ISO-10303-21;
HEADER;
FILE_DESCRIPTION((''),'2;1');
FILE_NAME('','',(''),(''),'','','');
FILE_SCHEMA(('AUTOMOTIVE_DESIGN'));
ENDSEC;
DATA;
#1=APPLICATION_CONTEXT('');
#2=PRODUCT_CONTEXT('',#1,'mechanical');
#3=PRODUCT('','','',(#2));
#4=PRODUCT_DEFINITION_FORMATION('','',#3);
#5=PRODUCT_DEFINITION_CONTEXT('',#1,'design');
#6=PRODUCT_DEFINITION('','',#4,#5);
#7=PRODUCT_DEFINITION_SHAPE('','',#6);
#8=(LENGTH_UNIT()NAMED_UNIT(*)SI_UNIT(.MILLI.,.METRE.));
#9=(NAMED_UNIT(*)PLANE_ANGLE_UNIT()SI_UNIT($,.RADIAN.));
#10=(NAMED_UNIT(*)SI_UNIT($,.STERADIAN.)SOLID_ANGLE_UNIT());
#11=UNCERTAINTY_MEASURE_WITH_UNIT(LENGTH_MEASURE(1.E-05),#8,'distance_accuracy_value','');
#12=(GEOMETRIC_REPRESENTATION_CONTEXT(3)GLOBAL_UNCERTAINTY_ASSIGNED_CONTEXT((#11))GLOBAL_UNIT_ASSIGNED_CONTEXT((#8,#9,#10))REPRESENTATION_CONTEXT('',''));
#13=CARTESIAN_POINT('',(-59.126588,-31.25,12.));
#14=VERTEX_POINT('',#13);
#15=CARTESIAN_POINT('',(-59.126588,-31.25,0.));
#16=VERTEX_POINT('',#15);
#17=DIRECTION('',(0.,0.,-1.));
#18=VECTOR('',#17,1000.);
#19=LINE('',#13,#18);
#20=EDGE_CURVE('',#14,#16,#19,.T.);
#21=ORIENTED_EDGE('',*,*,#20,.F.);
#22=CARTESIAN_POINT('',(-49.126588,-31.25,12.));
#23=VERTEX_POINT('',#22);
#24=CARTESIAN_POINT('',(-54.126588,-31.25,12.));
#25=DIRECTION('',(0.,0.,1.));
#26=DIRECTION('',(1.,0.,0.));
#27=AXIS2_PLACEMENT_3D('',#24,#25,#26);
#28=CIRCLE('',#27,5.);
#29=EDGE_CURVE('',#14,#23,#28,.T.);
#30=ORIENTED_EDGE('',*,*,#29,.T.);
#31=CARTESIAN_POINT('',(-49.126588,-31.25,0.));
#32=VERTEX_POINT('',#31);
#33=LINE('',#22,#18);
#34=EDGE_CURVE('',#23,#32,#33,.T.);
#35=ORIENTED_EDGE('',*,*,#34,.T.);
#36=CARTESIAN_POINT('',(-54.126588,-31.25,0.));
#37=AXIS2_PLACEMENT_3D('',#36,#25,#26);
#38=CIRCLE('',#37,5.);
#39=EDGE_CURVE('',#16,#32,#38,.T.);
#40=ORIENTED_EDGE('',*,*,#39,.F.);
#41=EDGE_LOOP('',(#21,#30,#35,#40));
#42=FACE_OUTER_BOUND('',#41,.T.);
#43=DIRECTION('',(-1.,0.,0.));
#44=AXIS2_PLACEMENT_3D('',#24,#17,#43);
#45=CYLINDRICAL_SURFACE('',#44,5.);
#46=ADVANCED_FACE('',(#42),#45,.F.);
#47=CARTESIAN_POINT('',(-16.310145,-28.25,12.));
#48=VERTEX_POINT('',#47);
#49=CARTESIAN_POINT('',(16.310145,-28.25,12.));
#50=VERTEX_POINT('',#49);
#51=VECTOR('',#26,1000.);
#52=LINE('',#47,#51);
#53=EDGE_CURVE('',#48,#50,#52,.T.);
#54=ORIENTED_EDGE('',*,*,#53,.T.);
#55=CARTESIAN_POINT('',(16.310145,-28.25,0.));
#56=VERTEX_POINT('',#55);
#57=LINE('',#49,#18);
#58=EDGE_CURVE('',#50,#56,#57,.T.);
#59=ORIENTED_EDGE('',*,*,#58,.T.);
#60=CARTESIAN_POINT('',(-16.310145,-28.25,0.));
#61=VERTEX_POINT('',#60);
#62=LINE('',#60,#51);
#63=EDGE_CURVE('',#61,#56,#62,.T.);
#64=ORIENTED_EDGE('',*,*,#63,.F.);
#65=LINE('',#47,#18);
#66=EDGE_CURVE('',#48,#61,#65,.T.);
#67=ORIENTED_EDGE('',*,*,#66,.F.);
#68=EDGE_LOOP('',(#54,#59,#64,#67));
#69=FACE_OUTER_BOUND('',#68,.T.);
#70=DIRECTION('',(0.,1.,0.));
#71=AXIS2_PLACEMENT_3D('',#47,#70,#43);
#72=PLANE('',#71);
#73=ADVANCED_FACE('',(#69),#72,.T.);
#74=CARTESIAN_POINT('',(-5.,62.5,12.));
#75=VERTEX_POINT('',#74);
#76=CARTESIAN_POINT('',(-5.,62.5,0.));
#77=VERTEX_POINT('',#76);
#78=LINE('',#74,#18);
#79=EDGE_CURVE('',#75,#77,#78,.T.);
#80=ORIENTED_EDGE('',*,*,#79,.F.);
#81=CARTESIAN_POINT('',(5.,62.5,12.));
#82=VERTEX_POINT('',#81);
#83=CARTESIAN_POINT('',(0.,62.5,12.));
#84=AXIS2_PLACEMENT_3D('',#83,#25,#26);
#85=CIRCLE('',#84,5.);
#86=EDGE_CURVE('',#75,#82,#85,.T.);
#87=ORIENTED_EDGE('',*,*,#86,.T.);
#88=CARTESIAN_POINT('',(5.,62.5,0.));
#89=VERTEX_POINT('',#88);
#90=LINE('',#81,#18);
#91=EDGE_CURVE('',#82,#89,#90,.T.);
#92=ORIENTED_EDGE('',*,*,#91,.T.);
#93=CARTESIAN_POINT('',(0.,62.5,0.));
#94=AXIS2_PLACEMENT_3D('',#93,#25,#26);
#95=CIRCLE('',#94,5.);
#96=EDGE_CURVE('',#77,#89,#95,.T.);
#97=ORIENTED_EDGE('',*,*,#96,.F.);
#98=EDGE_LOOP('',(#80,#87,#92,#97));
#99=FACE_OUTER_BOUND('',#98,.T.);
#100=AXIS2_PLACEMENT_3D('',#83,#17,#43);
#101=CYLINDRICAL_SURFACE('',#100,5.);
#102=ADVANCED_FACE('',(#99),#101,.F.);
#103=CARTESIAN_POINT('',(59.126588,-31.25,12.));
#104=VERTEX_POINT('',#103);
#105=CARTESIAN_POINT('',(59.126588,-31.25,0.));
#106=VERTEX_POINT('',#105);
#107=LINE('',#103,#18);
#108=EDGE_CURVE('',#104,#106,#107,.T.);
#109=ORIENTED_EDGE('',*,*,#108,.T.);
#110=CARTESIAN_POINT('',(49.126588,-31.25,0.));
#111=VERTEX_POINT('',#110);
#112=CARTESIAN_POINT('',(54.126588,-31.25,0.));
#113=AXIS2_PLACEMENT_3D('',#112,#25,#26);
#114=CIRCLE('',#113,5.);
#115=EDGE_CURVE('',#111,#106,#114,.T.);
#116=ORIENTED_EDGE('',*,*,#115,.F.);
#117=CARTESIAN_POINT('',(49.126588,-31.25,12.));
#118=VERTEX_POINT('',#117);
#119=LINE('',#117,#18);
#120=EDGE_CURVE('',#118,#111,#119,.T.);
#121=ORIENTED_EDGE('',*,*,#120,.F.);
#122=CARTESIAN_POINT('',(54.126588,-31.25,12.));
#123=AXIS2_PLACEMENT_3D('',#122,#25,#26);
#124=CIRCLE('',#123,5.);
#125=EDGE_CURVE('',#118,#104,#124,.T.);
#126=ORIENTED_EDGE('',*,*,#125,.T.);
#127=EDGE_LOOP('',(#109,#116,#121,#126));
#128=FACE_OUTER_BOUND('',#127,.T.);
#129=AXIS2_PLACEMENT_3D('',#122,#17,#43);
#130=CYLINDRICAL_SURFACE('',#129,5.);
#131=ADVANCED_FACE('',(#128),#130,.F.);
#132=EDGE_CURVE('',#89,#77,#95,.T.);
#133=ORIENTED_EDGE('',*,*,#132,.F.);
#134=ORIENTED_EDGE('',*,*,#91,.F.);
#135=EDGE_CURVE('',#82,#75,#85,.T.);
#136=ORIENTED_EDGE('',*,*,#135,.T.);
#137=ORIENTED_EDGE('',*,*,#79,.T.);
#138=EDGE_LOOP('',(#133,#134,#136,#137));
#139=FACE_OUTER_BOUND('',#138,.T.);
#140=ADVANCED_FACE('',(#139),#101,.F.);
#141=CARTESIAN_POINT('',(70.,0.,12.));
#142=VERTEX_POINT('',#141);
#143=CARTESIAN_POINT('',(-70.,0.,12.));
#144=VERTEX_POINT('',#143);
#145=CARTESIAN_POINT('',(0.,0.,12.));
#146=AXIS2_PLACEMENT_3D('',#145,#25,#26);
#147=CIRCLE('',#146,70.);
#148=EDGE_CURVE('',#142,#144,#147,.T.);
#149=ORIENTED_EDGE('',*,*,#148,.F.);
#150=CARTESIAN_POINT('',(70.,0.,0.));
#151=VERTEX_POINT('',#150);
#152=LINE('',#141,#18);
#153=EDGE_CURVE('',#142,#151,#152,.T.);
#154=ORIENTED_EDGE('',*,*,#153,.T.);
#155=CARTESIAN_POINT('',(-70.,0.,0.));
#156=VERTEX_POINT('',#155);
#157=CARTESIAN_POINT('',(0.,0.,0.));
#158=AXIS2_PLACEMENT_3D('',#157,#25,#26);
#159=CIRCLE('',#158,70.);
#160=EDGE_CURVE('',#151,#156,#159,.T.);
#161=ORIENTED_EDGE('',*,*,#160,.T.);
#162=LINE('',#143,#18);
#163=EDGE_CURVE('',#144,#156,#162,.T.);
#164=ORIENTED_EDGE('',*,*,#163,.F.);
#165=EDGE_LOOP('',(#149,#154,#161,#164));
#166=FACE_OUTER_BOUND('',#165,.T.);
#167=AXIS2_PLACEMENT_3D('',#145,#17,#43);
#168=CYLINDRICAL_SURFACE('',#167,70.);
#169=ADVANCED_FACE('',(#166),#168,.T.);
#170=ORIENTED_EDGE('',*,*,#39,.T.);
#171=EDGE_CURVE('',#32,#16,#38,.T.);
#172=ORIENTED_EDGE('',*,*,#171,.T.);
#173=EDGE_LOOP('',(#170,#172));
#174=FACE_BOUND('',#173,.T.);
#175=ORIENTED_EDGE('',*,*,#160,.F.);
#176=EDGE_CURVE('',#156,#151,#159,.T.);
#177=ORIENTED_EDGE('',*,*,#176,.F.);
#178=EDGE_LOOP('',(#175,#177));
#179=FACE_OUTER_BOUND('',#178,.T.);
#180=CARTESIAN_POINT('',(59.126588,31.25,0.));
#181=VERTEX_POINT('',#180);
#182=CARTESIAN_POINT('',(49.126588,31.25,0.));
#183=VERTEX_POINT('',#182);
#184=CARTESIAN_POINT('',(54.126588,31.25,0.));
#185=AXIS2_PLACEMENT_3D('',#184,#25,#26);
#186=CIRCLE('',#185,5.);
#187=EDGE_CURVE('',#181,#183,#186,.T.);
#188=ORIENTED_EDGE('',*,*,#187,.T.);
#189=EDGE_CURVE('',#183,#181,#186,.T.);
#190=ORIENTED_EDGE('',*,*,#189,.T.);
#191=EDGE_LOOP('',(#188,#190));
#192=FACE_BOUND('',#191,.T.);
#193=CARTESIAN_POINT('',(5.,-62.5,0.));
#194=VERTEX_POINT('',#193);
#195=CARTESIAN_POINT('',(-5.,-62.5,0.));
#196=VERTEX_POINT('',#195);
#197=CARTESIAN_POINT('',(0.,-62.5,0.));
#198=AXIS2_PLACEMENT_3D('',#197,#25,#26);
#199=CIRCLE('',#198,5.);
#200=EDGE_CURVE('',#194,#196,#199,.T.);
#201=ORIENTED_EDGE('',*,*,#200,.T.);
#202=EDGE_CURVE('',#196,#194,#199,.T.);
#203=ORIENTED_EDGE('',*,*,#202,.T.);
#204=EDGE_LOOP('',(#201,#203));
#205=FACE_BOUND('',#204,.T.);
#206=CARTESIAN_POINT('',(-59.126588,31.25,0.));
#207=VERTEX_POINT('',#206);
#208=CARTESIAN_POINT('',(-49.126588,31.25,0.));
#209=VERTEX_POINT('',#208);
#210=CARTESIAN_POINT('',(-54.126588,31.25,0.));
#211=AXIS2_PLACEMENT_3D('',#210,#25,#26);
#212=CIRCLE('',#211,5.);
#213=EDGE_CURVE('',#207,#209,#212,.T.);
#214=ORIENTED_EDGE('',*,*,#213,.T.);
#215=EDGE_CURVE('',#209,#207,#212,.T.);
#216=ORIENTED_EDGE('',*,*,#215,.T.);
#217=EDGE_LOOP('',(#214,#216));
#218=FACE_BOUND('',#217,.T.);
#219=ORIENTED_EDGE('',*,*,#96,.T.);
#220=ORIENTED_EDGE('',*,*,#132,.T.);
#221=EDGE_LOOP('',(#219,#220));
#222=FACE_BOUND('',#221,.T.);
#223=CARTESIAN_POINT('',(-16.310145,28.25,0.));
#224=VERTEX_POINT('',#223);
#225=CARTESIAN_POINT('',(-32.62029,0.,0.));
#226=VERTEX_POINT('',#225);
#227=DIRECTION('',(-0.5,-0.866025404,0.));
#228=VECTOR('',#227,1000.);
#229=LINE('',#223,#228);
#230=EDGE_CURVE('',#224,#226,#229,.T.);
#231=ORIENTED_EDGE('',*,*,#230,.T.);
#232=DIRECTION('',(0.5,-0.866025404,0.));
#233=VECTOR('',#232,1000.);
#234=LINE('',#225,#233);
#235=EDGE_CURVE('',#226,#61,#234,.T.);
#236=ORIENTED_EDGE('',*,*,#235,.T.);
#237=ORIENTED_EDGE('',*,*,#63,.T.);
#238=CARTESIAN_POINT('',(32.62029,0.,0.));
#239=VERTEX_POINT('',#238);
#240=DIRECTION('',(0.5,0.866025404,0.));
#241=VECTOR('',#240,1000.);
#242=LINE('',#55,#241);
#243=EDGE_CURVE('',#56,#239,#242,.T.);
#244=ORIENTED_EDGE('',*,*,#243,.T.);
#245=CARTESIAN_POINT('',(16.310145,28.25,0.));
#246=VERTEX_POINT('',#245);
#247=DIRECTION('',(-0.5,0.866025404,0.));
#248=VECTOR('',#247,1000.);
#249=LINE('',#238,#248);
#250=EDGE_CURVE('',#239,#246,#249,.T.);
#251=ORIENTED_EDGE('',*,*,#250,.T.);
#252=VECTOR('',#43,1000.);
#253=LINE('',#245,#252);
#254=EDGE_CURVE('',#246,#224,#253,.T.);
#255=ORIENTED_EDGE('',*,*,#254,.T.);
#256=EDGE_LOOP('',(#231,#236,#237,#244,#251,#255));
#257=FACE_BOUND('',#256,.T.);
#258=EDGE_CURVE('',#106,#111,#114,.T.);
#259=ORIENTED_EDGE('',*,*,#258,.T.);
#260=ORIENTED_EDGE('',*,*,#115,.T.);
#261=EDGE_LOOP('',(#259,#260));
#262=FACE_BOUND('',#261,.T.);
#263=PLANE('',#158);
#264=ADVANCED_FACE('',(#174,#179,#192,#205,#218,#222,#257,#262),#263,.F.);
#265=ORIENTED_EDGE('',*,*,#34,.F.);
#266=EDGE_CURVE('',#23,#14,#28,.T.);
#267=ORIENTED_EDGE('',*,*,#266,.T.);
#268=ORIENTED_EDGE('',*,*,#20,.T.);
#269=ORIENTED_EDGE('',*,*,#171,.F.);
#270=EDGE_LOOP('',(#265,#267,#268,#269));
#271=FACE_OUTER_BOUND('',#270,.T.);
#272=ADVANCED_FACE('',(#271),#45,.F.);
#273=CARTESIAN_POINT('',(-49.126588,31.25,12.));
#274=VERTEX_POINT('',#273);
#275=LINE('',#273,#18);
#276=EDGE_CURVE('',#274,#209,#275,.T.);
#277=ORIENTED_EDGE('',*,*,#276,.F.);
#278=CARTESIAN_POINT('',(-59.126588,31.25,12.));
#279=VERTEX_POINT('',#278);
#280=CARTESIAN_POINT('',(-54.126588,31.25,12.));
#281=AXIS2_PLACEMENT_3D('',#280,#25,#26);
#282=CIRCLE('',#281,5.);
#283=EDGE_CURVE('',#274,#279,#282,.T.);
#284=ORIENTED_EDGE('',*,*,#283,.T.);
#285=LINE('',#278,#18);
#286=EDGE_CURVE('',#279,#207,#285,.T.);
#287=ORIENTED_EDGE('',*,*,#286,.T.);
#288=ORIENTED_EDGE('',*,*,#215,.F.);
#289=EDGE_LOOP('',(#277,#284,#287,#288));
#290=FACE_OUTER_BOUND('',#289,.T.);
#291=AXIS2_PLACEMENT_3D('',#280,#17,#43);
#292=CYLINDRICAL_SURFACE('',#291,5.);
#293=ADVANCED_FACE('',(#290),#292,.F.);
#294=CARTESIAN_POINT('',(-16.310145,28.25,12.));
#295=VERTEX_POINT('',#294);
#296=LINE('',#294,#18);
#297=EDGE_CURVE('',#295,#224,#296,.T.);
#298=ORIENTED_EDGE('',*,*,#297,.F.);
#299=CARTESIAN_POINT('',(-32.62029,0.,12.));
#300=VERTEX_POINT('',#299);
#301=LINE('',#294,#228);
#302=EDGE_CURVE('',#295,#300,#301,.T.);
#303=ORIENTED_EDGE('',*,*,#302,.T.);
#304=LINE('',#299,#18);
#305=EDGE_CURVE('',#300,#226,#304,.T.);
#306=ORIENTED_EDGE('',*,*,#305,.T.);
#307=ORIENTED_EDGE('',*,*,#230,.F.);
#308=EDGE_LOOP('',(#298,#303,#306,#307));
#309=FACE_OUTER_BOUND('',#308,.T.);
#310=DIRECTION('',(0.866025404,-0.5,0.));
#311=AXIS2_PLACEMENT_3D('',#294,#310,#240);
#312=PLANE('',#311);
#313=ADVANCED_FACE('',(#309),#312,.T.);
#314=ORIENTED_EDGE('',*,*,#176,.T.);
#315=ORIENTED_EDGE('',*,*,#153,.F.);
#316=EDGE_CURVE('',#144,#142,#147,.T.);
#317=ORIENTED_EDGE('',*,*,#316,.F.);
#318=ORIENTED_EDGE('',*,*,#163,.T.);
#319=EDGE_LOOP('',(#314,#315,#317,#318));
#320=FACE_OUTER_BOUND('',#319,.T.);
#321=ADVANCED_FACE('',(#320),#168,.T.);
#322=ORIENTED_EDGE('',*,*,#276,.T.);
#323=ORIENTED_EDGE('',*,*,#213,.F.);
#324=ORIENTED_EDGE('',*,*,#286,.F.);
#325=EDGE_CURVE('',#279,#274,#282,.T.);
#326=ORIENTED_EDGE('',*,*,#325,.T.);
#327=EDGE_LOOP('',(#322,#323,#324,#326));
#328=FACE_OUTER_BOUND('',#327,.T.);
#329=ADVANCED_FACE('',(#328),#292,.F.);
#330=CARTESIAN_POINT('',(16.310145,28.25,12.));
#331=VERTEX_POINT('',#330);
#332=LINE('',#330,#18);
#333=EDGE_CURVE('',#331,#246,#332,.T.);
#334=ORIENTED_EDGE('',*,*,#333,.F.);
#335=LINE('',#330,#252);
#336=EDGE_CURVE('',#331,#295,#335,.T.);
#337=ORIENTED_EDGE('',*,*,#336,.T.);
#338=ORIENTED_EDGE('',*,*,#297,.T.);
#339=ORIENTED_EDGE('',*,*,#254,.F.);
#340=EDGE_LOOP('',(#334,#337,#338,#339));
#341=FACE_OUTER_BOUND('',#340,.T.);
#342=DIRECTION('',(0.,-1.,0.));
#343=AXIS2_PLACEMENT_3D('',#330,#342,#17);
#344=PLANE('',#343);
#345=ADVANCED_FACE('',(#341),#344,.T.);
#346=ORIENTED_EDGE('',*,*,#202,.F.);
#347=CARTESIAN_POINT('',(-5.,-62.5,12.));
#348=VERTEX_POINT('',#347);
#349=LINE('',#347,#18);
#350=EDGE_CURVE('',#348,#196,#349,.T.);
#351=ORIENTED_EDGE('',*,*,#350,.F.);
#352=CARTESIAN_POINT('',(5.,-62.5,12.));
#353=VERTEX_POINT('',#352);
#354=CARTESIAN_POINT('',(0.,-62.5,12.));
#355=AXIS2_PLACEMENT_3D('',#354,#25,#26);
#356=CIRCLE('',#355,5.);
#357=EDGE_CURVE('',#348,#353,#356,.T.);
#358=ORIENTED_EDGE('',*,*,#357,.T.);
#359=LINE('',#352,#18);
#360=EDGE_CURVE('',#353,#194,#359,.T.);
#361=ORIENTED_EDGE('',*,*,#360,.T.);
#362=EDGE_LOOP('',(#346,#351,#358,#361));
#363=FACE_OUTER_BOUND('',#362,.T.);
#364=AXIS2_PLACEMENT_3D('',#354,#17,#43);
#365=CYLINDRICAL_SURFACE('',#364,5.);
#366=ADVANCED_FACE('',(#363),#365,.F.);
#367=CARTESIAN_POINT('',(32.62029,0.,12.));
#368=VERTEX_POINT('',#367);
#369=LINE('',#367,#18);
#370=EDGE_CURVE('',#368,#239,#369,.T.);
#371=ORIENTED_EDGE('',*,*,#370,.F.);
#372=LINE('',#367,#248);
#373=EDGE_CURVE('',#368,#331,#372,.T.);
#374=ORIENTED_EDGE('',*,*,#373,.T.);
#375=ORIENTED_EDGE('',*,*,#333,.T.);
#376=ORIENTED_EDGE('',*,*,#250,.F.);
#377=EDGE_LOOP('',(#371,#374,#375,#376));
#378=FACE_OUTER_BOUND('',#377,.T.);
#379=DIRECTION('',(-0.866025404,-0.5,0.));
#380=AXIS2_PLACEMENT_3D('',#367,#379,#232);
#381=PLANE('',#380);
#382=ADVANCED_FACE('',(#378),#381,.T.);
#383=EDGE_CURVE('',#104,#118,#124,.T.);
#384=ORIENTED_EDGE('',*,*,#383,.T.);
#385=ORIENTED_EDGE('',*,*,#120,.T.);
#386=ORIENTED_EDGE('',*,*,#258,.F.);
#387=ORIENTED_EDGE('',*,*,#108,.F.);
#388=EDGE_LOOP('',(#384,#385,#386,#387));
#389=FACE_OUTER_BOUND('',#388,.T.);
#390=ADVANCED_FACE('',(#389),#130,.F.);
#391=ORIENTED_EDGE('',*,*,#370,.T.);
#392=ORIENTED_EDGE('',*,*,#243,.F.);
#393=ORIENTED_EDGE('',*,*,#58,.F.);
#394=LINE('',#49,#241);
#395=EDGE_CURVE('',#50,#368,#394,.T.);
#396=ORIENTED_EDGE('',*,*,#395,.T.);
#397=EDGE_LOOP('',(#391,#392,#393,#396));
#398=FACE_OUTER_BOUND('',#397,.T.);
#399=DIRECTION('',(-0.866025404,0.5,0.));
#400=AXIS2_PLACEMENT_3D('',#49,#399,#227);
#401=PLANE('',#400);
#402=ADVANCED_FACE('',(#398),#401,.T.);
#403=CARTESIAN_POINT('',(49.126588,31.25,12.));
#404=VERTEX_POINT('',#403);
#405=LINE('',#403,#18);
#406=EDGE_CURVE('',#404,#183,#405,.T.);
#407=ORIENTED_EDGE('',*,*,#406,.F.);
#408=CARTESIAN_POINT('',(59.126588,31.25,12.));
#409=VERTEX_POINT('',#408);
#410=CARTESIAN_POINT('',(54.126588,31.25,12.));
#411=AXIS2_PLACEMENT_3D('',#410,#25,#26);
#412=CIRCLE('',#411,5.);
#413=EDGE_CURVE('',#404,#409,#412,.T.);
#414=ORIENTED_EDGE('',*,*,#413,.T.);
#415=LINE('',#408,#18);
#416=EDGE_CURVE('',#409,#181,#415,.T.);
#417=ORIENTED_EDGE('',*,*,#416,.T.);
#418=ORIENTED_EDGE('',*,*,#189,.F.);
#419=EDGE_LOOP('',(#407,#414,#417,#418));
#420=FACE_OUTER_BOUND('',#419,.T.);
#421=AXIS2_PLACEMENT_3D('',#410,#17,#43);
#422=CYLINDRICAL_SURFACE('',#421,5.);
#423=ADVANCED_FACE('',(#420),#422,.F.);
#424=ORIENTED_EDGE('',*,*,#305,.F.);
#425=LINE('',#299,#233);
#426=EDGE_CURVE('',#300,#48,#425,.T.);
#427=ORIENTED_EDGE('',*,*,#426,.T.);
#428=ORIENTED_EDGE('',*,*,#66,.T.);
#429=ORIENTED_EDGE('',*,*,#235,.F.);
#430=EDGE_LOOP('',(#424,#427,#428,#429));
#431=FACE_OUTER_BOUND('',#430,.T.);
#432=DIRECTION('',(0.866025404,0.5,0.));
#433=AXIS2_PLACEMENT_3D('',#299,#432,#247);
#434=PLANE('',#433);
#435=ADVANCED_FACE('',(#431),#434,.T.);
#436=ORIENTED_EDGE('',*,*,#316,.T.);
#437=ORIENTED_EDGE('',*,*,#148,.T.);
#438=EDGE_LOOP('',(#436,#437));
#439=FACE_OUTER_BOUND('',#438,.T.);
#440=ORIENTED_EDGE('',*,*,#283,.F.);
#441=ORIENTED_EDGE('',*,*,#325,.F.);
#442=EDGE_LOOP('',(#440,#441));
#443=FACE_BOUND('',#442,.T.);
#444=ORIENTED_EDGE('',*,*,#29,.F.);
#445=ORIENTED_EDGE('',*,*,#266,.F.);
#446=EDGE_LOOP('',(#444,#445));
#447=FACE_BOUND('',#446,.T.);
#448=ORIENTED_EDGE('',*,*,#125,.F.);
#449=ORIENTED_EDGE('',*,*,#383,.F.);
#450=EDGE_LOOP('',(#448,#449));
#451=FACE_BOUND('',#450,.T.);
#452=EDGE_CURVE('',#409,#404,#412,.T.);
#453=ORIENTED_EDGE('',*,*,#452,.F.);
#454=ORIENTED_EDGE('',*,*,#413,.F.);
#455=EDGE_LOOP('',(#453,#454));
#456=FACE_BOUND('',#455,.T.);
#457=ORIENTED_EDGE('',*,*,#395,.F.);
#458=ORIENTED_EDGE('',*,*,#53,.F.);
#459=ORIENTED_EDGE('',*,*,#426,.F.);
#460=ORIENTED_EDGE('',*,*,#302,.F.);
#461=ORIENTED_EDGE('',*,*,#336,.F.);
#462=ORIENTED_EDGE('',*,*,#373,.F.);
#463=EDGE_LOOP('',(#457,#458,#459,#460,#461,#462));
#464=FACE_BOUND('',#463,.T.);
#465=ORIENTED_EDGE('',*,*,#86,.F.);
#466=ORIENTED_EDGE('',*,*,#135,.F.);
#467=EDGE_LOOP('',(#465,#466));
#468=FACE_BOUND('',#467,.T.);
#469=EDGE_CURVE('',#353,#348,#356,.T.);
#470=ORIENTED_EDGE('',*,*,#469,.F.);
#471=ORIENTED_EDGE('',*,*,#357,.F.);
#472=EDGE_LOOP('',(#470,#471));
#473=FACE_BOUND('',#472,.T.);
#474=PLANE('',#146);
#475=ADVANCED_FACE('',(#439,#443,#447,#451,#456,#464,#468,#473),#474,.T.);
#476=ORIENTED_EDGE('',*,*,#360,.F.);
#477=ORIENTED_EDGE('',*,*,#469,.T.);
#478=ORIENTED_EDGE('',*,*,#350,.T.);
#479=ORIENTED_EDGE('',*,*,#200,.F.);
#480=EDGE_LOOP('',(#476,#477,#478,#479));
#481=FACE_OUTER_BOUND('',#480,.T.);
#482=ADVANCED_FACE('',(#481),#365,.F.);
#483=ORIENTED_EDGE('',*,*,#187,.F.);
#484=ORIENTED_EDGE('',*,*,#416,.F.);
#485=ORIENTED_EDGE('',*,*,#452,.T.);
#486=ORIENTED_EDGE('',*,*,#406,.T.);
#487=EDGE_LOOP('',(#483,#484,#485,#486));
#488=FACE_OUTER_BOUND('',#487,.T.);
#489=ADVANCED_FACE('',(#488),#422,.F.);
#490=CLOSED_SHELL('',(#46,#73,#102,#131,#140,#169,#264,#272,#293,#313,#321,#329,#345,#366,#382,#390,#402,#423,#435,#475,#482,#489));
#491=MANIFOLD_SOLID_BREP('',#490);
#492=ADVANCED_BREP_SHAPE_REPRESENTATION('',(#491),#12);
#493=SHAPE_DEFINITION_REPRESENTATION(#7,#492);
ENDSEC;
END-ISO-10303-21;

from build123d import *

# Parameters (mm, degrees)
SKETCH1_R           = 70
SKETCH1_R_2         = 5
BOSS_EXTRUDE1_DEPTH = 12


with BuildPart() as part:
    # Sketch1 → Boss-Extrude1 (new body)
    with BuildSketch(Plane.XY):
        Circle(SKETCH1_R)
        with Locations((0, 62.5)):
            Circle(SKETCH1_R_2, mode=Mode.SUBTRACT)
        with Locations((54.126587737, 31.25)):
            Circle(SKETCH1_R_2, mode=Mode.SUBTRACT)
        with Locations((54.126587737, -31.25)):
            Circle(SKETCH1_R_2, mode=Mode.SUBTRACT)
        with Locations((0, -62.5)):
            Circle(SKETCH1_R_2, mode=Mode.SUBTRACT)
        with Locations((-54.126587737, -31.25)):
            Circle(SKETCH1_R_2, mode=Mode.SUBTRACT)
        with Locations((-54.126587737, 31.25)):
            Circle(SKETCH1_R_2, mode=Mode.SUBTRACT)
        Polygon((32.620290209, 0), (16.310145105, 28.25), (-16.310145105, 28.25), (-32.620290209, 0), (-16.310145105, -28.25), (16.310145105, -28.25), align=None, mode=Mode.SUBTRACT)
    extrude(amount=BOSS_EXTRUDE1_DEPTH)


solid = part.part
